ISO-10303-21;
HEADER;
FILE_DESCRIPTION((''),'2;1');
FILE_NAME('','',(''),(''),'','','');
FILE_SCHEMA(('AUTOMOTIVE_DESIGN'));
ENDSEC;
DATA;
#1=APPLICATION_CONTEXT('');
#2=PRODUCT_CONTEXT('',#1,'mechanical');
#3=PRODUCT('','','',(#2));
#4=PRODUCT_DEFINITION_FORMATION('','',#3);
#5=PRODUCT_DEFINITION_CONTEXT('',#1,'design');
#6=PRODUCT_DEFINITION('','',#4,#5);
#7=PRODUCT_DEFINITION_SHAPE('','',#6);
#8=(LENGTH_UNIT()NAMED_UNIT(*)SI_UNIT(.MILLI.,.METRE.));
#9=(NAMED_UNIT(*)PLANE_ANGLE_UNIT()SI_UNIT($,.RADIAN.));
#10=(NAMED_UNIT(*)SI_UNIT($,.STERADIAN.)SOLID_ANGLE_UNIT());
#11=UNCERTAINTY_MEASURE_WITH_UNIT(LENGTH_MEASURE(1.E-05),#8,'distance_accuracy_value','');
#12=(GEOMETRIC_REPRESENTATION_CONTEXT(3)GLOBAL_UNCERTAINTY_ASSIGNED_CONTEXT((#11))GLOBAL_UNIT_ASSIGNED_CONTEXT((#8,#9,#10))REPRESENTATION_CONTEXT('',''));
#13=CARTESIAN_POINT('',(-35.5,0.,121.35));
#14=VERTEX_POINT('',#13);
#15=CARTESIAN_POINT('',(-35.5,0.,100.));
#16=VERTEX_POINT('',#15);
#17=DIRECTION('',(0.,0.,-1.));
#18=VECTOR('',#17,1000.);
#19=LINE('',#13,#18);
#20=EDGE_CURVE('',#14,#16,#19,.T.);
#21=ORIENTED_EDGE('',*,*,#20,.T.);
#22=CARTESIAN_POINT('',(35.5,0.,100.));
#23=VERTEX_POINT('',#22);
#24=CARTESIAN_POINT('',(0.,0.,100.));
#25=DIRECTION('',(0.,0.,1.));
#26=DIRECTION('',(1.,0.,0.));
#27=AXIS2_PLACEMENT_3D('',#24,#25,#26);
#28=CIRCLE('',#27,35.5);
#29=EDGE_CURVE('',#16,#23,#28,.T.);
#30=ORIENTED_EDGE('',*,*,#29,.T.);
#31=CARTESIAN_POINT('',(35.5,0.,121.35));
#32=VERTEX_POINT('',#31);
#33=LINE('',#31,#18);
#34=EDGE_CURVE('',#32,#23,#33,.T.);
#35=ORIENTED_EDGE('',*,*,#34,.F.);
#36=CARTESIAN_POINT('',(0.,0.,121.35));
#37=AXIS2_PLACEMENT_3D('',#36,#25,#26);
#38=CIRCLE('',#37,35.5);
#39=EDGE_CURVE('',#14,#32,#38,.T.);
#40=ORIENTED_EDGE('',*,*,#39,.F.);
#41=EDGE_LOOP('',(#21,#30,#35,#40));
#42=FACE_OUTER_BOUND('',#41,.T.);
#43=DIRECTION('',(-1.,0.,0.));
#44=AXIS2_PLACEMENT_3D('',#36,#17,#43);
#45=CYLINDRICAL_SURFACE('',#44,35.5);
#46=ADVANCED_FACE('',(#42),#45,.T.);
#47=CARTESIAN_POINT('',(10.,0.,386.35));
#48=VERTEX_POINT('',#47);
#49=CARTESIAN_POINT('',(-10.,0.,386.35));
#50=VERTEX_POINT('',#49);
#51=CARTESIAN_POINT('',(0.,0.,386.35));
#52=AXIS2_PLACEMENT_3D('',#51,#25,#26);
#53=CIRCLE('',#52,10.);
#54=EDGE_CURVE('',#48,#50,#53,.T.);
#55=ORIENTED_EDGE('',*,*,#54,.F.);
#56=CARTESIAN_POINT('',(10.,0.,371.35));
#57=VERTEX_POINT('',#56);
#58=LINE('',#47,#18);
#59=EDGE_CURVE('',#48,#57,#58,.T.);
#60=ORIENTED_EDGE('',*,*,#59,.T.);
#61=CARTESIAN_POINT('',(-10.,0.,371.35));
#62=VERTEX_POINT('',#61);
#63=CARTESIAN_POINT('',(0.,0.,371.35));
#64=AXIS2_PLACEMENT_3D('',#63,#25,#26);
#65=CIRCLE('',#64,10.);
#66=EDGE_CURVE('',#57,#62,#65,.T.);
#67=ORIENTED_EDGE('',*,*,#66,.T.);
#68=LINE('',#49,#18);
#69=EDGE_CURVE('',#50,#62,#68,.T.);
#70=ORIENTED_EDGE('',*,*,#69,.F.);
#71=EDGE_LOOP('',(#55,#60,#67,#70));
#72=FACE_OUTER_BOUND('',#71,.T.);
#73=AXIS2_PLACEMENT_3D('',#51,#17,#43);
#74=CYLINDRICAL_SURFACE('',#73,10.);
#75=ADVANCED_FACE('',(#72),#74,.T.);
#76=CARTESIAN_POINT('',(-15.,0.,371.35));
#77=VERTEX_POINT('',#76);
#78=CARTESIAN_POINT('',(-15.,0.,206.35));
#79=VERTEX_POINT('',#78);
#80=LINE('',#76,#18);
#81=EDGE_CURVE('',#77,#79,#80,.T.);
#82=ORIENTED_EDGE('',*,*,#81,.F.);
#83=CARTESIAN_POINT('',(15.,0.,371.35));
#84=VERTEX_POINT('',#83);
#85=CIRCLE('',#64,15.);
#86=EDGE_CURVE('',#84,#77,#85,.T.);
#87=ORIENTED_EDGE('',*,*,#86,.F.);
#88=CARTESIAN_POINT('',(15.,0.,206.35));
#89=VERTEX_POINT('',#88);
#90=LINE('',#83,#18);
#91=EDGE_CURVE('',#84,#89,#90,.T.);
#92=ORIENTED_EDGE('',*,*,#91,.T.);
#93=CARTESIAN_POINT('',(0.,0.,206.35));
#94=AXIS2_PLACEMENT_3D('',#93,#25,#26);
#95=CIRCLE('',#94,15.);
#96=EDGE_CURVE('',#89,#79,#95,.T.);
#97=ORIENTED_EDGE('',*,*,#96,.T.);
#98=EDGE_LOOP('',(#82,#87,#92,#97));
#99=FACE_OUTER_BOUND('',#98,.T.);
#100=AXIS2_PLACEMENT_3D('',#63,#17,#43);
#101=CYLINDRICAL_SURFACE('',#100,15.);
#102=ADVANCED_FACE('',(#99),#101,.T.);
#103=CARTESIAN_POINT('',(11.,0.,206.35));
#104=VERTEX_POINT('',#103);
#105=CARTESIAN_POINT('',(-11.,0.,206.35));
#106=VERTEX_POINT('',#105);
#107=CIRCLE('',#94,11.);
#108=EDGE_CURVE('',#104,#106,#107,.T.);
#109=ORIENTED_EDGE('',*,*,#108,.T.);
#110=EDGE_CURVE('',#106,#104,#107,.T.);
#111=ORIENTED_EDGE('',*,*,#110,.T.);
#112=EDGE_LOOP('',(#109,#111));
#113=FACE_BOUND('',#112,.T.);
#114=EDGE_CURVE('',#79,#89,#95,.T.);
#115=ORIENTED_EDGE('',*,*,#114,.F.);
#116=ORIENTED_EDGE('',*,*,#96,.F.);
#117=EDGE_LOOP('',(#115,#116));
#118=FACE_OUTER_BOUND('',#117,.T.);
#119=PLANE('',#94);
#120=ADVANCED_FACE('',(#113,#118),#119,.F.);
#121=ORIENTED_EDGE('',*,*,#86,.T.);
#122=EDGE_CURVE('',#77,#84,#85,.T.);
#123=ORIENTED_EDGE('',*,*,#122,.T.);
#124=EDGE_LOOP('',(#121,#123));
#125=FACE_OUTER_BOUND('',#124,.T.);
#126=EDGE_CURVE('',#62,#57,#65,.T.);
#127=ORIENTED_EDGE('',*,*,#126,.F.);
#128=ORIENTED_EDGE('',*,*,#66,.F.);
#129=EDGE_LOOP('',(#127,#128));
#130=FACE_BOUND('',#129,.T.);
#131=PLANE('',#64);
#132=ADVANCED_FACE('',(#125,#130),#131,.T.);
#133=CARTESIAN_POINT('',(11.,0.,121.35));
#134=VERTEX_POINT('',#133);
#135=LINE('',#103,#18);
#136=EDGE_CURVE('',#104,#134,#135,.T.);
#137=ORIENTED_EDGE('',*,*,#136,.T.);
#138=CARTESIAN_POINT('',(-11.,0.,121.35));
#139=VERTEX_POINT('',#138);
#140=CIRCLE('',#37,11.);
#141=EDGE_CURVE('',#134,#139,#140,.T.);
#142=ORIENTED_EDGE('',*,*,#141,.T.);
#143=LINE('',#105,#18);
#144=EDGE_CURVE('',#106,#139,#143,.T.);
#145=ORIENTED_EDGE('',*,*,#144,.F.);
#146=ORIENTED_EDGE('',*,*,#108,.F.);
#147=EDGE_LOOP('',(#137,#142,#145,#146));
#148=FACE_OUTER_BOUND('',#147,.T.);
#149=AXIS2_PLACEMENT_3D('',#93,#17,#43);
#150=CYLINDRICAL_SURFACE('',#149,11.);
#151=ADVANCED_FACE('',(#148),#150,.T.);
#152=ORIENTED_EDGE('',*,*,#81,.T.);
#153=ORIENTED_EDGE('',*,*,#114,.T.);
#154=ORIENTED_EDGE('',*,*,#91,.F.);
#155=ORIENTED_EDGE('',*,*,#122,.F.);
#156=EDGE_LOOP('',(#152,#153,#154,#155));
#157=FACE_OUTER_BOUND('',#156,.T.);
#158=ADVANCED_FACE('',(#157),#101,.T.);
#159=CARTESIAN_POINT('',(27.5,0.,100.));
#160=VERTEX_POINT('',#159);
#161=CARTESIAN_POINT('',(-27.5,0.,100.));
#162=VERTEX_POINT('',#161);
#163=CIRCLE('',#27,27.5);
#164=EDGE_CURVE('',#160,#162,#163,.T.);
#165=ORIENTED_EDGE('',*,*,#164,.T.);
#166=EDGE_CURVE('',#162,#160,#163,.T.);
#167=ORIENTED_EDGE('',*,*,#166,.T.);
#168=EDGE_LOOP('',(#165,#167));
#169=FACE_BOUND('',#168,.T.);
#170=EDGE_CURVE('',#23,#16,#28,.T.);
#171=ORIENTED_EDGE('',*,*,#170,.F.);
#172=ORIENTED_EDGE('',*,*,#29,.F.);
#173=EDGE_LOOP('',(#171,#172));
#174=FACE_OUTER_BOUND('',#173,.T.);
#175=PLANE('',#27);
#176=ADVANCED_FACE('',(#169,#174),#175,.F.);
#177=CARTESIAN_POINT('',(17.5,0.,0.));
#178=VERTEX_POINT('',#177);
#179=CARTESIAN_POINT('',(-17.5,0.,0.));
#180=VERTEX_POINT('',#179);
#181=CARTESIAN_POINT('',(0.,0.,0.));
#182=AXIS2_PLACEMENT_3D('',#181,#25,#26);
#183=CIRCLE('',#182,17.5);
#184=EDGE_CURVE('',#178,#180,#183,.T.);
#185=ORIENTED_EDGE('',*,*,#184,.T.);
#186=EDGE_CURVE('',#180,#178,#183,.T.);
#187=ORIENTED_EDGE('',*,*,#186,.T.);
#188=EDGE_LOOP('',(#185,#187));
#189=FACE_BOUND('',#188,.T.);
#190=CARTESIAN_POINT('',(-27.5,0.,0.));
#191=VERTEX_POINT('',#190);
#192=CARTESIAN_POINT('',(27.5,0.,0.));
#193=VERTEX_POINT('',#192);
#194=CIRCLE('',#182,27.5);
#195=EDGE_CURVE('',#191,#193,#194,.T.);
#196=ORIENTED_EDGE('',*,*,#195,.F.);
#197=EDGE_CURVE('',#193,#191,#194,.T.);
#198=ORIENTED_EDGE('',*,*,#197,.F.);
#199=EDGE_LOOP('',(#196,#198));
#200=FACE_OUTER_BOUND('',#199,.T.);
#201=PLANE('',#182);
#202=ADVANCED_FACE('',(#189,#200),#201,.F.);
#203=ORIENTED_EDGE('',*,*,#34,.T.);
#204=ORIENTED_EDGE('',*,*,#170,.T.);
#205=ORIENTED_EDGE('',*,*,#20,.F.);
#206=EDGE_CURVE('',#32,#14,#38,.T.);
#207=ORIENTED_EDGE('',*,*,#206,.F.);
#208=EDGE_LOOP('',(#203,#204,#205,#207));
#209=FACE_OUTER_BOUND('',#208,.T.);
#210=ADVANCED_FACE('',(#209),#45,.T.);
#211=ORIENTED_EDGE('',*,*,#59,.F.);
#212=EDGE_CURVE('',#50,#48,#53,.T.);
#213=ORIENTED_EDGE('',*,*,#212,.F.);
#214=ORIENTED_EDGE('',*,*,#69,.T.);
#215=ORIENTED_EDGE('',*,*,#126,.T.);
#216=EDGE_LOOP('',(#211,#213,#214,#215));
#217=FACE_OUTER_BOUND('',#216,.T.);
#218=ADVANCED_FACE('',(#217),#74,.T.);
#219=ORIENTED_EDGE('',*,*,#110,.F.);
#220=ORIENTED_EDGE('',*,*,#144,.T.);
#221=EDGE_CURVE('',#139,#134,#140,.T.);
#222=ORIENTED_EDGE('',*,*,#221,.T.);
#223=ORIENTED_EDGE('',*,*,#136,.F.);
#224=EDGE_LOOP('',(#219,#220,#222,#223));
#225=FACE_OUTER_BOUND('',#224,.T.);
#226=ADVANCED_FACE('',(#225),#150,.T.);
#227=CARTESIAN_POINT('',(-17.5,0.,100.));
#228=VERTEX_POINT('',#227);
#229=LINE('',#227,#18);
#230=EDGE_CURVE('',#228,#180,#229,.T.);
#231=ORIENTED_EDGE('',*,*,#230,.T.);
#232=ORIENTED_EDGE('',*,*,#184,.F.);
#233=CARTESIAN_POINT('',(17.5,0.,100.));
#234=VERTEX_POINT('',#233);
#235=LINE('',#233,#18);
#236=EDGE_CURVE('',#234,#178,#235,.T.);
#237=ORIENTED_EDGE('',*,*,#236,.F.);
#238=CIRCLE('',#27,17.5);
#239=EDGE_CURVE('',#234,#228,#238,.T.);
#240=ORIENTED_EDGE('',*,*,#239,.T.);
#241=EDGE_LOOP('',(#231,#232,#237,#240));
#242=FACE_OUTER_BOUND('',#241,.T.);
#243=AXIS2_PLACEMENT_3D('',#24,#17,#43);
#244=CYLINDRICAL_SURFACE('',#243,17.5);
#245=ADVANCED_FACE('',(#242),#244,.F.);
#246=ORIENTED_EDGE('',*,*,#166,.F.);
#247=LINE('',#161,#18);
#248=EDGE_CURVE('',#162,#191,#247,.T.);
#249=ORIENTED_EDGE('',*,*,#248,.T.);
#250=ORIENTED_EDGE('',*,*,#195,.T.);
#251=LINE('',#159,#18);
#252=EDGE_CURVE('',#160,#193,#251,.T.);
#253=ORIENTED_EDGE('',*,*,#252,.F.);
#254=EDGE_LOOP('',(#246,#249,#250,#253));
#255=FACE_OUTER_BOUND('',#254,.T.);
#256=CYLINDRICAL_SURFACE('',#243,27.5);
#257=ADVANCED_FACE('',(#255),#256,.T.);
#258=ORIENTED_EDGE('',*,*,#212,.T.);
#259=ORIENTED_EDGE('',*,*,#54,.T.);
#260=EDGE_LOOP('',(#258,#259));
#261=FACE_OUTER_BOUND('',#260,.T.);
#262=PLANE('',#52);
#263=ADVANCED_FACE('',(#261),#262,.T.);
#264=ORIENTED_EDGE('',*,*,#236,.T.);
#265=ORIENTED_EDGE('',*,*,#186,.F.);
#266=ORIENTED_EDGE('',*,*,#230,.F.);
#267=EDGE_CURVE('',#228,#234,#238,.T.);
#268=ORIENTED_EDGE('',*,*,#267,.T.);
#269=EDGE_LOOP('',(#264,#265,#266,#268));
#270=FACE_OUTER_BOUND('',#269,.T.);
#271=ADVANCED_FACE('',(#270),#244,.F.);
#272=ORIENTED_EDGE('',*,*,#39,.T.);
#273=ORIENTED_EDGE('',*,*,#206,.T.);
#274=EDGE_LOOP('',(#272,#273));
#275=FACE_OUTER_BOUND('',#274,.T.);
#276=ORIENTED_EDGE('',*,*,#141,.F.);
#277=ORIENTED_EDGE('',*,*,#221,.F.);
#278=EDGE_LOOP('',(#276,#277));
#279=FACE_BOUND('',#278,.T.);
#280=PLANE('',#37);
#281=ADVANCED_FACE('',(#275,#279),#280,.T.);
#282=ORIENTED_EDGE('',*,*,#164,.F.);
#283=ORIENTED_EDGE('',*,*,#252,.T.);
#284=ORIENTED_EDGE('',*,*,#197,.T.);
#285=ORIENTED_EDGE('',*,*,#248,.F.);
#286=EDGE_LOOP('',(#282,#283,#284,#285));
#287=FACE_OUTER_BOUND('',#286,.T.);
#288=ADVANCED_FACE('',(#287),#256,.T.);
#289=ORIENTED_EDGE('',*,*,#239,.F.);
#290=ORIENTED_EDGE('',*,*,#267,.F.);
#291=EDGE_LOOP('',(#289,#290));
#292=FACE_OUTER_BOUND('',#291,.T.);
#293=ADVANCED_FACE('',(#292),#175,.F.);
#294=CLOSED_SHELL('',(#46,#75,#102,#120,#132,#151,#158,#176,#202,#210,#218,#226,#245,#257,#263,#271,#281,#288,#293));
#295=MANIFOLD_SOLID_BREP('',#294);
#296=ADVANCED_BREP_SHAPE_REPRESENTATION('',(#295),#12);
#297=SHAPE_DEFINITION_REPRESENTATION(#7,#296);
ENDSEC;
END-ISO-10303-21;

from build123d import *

# Parameters (mm, degrees)
SKETCH1_R           = 27.5
SKETCH1_R_2         = 17.5
BOSS_EXTRUDE1_DEPTH = 100
SKETCH2_R           = 35.5
BOSS_EXTRUDE2_DEPTH = 21.35
SKETCH3_R           = 11
BOSS_EXTRUDE3_DEPTH = 85
SKETCH4_R           = 15
BOSS_EXTRUDE4_DEPTH = 165
SKETCH5_R           = 10
BOSS_EXTRUDE5_DEPTH = 15


with BuildPart() as part:
    # Sketch1 → Boss-Extrude1 (new body)
    with BuildSketch(Plane.XY):
        Circle(SKETCH1_R)
        Circle(SKETCH1_R_2, mode=Mode.SUBTRACT)
    extrude(amount=BOSS_EXTRUDE1_DEPTH)

    # Sketch2 → Boss-Extrude2 (add)
    with BuildSketch(Plane.XY.offset(100)):
        with Locations(Location((0, 0, 0), (0, 0, 180))):
            Circle(SKETCH2_R)
    extrude(amount=BOSS_EXTRUDE2_DEPTH)

    # Sketch3 → Boss-Extrude3 (add)
    with BuildSketch(Plane.XY.offset(121.35)):
        Circle(SKETCH3_R)
    extrude(amount=BOSS_EXTRUDE3_DEPTH)

    # Sketch4 → Boss-Extrude4 (add)
    with BuildSketch(Plane.XY.offset(206.35)):
        Circle(SKETCH4_R)
    extrude(amount=BOSS_EXTRUDE4_DEPTH)

    # Sketch5 → Boss-Extrude5 (add)
    with BuildSketch(Plane.XY.offset(371.35)):
        Circle(SKETCH5_R)
    extrude(amount=BOSS_EXTRUDE5_DEPTH)


solid = part.part
